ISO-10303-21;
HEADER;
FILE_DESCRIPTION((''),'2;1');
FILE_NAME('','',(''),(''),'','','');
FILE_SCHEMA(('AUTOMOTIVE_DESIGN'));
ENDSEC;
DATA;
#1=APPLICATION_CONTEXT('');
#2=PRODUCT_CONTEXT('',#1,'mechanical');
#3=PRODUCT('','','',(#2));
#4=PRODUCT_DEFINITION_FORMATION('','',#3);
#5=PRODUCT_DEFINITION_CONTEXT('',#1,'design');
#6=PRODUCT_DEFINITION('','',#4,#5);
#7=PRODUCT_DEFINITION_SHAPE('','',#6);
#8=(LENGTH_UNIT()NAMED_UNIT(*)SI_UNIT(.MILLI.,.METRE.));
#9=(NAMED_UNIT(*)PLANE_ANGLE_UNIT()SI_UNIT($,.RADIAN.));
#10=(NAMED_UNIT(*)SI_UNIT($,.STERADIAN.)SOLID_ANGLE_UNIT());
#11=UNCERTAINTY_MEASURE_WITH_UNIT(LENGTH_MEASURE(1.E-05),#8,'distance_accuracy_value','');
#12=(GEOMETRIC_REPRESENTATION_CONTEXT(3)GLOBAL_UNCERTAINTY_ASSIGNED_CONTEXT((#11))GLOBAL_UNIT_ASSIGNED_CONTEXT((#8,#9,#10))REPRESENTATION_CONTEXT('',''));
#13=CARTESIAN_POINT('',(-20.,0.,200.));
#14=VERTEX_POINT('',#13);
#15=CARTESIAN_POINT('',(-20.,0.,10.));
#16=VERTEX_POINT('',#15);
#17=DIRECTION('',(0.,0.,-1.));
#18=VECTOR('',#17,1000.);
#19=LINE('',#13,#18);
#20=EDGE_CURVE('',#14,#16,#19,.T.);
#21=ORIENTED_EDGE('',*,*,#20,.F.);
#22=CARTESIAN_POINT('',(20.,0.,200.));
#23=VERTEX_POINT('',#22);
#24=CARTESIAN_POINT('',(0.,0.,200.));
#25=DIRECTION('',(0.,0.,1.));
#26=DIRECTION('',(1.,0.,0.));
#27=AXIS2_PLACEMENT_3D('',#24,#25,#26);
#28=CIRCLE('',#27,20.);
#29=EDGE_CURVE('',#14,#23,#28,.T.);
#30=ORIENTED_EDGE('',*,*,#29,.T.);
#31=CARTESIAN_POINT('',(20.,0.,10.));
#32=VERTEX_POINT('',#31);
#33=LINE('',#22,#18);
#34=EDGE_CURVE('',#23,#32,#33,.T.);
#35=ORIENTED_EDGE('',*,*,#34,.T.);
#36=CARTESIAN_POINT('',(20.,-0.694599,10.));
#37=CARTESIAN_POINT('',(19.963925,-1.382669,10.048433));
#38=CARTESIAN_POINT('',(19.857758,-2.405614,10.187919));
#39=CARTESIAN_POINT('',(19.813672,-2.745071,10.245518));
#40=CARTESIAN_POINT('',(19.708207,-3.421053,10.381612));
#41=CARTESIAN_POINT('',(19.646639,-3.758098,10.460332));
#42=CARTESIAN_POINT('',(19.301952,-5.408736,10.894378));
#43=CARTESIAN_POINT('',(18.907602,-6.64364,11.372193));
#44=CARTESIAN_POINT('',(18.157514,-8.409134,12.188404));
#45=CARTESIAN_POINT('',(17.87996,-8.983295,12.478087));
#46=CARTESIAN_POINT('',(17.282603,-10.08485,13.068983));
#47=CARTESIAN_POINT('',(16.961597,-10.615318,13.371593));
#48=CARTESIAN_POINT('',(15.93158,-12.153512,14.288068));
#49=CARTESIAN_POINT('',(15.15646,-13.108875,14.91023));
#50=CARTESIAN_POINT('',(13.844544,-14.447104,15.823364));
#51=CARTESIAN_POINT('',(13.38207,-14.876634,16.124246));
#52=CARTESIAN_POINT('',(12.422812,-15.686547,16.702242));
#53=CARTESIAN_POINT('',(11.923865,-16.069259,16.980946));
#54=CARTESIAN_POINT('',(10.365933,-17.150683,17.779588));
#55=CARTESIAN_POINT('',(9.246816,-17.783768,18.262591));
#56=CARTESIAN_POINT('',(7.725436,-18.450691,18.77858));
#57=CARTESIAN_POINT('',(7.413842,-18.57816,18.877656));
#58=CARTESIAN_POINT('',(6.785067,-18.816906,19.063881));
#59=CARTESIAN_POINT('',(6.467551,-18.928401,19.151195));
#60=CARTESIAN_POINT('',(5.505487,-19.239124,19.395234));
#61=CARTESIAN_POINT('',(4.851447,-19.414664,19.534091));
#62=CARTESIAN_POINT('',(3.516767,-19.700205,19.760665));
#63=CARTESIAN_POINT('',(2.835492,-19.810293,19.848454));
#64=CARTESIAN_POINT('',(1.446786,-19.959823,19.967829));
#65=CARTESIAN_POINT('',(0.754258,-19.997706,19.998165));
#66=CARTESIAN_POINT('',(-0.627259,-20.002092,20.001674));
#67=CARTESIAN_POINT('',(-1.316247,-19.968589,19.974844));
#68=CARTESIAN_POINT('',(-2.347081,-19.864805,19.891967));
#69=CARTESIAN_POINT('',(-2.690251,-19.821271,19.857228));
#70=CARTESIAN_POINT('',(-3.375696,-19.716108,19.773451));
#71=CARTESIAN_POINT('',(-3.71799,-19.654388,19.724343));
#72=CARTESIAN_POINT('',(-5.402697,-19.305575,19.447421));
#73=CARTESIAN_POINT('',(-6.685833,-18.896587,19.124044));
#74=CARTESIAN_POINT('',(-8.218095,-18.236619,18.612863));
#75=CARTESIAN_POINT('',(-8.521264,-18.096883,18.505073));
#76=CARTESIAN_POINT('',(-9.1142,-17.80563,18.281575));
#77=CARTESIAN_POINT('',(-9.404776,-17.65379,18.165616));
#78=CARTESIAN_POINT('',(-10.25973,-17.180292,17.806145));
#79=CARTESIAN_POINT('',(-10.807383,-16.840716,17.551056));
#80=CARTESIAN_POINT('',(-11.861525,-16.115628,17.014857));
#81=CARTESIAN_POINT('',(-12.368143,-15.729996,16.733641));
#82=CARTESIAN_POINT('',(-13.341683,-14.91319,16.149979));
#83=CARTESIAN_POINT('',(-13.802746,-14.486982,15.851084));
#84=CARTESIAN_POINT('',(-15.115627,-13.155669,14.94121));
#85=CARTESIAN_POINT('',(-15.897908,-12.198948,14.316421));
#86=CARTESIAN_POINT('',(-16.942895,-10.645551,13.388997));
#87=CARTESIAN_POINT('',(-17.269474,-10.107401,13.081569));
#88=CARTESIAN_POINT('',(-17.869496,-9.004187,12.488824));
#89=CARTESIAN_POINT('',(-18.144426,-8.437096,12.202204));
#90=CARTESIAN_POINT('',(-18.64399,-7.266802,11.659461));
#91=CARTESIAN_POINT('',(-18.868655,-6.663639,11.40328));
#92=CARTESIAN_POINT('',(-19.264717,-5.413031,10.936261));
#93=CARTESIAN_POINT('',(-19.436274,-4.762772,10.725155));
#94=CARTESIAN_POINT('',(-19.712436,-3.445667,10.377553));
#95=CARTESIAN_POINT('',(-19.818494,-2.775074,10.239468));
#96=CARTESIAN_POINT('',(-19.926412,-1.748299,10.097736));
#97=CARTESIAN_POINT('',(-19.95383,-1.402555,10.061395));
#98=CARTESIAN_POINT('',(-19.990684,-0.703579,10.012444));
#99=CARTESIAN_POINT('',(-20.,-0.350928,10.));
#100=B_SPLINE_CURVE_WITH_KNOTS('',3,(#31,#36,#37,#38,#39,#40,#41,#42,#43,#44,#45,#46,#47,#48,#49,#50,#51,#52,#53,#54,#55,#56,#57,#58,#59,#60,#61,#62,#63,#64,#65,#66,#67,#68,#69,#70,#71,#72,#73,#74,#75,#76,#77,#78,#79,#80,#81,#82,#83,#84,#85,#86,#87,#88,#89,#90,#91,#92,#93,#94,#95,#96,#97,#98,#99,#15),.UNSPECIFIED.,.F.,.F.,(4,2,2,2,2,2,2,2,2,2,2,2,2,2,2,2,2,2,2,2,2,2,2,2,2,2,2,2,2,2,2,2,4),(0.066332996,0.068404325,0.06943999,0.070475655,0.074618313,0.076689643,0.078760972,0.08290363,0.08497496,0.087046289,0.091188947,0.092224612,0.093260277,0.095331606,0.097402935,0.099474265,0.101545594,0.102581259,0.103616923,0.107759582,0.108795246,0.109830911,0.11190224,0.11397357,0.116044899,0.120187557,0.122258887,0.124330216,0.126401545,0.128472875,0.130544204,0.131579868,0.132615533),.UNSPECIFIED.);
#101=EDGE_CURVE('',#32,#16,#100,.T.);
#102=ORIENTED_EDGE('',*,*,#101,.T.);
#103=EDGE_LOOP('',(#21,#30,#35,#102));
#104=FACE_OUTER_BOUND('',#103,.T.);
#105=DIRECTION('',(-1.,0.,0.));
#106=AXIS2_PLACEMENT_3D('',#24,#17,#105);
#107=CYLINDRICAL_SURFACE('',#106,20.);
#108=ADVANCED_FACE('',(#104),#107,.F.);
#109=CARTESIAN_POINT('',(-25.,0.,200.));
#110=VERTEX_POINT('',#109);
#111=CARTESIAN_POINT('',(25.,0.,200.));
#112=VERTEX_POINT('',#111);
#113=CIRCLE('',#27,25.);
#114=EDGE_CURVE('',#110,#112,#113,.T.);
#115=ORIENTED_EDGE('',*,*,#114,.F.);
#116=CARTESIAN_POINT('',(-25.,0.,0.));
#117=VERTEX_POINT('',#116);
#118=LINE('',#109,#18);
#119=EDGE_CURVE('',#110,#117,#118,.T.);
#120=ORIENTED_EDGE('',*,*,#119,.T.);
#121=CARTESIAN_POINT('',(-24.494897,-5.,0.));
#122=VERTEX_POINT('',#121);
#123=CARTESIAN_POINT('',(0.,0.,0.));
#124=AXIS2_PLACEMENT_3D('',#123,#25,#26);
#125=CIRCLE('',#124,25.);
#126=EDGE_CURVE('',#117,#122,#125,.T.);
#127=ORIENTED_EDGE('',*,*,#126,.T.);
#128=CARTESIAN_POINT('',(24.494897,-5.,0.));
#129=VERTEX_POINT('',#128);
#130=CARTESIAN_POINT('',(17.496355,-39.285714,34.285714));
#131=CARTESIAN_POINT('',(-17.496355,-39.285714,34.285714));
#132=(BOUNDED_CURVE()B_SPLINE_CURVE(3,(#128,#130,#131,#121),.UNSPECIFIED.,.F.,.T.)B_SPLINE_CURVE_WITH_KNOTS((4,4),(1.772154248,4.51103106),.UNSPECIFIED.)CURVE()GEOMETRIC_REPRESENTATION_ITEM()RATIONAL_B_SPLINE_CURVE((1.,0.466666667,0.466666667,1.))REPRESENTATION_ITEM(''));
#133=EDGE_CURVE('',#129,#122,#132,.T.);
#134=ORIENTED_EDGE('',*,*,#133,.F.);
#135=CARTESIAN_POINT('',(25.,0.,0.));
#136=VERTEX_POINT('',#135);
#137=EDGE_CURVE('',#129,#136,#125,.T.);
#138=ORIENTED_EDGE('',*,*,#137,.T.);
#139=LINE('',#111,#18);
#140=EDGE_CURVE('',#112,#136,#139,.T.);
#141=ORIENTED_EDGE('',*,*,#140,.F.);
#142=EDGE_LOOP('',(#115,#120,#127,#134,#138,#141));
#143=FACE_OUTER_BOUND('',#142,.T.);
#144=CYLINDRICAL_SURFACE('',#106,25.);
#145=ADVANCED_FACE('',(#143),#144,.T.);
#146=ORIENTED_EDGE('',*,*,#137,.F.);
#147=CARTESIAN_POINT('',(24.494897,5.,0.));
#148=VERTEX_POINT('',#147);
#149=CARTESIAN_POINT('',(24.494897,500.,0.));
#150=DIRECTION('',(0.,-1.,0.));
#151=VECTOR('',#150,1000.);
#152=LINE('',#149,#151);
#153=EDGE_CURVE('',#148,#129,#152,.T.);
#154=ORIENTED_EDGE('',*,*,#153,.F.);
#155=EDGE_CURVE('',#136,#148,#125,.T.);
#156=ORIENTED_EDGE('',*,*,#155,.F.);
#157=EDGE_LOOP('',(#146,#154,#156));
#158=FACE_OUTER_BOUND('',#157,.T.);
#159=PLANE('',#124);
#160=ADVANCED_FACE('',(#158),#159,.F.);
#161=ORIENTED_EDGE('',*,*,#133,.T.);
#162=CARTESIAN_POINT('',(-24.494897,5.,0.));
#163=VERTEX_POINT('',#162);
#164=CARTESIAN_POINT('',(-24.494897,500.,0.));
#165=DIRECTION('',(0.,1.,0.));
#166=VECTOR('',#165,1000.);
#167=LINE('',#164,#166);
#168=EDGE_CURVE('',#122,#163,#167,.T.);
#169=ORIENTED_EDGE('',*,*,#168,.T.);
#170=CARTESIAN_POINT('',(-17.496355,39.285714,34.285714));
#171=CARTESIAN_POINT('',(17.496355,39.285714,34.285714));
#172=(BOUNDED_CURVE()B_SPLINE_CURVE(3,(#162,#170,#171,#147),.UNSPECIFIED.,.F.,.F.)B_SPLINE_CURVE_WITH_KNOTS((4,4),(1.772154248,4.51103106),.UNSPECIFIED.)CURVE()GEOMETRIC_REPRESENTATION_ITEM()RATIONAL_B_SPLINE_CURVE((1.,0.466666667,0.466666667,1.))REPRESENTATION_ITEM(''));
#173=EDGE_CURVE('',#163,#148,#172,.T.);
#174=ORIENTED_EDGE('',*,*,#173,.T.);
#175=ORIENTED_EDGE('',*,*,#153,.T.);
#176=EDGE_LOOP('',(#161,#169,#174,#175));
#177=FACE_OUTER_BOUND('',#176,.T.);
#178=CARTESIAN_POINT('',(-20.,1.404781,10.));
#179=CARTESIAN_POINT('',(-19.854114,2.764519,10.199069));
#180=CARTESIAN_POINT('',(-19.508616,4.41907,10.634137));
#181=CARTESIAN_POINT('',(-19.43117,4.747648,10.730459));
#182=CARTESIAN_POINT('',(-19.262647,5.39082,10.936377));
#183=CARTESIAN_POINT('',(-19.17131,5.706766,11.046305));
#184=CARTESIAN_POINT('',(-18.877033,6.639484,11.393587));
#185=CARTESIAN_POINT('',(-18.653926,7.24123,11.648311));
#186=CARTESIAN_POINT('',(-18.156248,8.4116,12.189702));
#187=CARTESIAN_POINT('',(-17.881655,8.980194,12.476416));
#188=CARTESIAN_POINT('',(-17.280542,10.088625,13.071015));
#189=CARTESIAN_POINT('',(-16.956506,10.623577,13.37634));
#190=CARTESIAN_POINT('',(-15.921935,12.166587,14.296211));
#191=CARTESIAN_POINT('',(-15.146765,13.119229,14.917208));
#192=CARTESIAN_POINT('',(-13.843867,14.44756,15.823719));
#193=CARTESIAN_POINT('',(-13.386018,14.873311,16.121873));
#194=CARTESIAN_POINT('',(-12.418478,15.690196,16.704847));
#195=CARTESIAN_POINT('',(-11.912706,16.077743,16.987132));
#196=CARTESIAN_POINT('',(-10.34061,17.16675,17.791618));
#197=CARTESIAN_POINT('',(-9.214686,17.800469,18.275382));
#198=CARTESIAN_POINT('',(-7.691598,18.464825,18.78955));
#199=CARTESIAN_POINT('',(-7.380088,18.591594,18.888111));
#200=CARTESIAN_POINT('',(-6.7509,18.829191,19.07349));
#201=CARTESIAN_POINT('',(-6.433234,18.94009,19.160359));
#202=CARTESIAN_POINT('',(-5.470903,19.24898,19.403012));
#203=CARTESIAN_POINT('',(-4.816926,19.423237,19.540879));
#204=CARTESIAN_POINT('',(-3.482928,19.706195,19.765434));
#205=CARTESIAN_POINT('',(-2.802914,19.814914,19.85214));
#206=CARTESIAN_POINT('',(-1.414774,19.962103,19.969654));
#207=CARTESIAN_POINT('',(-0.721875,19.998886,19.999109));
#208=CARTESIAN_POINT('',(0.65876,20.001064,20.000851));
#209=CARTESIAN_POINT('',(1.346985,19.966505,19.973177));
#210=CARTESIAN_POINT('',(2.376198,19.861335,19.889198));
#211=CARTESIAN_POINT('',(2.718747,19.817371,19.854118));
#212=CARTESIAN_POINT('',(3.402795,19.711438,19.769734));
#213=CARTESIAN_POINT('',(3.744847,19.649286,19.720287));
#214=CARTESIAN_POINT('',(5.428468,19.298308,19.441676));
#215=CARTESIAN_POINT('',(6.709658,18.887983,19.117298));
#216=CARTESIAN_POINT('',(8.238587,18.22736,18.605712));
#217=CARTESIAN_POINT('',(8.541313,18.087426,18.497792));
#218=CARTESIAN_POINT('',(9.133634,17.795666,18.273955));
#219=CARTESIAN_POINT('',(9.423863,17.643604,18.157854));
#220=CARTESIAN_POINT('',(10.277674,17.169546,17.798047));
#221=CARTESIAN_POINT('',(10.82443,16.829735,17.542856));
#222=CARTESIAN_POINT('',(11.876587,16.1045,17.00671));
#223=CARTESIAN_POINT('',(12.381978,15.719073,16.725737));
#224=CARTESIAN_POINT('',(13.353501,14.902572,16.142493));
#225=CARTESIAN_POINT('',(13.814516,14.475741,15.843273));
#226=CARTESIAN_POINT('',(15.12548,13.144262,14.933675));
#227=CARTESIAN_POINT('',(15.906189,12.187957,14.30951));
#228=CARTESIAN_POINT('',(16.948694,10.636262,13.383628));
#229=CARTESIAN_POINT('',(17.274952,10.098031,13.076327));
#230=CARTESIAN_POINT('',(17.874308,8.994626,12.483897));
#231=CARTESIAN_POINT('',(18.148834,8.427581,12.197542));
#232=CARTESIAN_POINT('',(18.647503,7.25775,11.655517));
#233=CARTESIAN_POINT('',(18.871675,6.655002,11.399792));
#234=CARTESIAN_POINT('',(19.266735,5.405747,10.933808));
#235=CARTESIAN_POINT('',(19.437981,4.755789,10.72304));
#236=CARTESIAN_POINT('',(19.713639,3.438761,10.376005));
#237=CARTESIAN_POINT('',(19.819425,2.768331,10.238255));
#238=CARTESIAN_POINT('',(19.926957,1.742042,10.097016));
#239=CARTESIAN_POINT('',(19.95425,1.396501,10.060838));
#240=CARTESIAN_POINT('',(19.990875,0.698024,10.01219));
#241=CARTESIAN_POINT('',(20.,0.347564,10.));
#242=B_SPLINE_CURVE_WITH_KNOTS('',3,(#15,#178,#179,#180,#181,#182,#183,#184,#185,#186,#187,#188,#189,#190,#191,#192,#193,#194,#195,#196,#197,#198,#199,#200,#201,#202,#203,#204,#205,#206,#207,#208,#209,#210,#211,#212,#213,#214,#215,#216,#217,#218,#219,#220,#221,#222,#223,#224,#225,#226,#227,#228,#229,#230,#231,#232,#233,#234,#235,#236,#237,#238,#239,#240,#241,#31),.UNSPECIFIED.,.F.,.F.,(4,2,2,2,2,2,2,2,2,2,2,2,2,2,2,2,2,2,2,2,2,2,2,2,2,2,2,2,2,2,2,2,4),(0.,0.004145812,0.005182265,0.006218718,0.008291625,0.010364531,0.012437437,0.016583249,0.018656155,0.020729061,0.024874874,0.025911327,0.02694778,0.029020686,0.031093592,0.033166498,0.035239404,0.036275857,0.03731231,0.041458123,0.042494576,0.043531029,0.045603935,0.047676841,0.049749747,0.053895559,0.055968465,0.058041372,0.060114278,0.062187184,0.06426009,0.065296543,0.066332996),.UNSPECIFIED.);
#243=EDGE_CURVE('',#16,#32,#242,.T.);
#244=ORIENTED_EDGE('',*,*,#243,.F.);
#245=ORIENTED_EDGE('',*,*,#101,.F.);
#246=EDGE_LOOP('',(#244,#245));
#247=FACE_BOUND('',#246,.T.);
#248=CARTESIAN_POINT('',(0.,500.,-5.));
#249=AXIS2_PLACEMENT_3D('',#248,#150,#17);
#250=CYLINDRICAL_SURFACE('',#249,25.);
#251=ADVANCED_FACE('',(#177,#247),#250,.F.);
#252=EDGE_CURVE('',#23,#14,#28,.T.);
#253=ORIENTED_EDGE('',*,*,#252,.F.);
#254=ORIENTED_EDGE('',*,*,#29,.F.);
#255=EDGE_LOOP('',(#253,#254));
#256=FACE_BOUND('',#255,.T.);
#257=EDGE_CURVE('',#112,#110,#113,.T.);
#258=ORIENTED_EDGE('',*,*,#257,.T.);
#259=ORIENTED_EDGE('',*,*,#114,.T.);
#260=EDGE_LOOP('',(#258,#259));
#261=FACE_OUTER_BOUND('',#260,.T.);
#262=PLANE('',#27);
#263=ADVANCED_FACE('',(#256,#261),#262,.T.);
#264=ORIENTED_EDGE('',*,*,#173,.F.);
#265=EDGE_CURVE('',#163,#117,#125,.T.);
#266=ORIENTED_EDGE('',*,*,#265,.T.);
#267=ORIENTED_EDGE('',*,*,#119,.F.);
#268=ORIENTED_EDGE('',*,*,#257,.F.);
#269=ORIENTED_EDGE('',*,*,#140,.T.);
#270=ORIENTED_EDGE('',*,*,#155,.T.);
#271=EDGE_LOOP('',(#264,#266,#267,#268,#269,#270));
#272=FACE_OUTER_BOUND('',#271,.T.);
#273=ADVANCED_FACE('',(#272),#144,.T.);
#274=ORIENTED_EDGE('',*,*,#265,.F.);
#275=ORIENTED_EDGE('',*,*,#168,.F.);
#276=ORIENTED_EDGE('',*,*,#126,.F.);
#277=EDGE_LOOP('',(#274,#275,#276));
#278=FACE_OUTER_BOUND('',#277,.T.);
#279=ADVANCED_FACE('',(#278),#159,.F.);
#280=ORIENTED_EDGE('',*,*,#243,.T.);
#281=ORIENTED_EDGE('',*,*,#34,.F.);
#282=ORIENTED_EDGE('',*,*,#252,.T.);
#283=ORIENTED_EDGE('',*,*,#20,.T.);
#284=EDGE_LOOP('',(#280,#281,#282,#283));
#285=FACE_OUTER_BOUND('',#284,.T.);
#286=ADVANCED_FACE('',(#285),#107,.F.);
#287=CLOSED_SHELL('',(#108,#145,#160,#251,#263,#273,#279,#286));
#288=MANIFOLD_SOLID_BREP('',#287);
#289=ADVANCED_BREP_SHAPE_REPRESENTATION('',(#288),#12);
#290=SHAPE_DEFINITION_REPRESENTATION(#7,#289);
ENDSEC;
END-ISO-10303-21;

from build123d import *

# Parameters (mm, degrees)
SKETCH_1_R               = 25
SKETCH_1_R_2             = 20
EXTRUDE_1_DEPTH          = 200
CUT_EXTRUDE_1_DEPTH      = 500
CUT_EXTRUDE_1_DEPTH_BACK = 204.100960116
SKETCH_2_R               = 25


with BuildPart() as part:
    # 草图1 → 凸台-拉伸1 (new body)
    with BuildSketch(Plane.XY):
        Circle(SKETCH_1_R)
        Circle(SKETCH_1_R_2, mode=Mode.SUBTRACT)
    extrude(amount=EXTRUDE_1_DEPTH)

    # 草图2 → 切除-拉伸1 (cut, two sides: drawn at the far end of the back side and taken through both)
    with BuildSketch(Plane(origin=(0, 0, 0), x_dir=(1, 0, 0), z_dir=(0, 1, 0)).offset(-CUT_EXTRUDE_1_DEPTH_BACK)):
        with Locations((0, 5)):
            Circle(SKETCH_2_R)
    extrude(amount=CUT_EXTRUDE_1_DEPTH + CUT_EXTRUDE_1_DEPTH_BACK, mode=Mode.SUBTRACT)


solid = part.part
